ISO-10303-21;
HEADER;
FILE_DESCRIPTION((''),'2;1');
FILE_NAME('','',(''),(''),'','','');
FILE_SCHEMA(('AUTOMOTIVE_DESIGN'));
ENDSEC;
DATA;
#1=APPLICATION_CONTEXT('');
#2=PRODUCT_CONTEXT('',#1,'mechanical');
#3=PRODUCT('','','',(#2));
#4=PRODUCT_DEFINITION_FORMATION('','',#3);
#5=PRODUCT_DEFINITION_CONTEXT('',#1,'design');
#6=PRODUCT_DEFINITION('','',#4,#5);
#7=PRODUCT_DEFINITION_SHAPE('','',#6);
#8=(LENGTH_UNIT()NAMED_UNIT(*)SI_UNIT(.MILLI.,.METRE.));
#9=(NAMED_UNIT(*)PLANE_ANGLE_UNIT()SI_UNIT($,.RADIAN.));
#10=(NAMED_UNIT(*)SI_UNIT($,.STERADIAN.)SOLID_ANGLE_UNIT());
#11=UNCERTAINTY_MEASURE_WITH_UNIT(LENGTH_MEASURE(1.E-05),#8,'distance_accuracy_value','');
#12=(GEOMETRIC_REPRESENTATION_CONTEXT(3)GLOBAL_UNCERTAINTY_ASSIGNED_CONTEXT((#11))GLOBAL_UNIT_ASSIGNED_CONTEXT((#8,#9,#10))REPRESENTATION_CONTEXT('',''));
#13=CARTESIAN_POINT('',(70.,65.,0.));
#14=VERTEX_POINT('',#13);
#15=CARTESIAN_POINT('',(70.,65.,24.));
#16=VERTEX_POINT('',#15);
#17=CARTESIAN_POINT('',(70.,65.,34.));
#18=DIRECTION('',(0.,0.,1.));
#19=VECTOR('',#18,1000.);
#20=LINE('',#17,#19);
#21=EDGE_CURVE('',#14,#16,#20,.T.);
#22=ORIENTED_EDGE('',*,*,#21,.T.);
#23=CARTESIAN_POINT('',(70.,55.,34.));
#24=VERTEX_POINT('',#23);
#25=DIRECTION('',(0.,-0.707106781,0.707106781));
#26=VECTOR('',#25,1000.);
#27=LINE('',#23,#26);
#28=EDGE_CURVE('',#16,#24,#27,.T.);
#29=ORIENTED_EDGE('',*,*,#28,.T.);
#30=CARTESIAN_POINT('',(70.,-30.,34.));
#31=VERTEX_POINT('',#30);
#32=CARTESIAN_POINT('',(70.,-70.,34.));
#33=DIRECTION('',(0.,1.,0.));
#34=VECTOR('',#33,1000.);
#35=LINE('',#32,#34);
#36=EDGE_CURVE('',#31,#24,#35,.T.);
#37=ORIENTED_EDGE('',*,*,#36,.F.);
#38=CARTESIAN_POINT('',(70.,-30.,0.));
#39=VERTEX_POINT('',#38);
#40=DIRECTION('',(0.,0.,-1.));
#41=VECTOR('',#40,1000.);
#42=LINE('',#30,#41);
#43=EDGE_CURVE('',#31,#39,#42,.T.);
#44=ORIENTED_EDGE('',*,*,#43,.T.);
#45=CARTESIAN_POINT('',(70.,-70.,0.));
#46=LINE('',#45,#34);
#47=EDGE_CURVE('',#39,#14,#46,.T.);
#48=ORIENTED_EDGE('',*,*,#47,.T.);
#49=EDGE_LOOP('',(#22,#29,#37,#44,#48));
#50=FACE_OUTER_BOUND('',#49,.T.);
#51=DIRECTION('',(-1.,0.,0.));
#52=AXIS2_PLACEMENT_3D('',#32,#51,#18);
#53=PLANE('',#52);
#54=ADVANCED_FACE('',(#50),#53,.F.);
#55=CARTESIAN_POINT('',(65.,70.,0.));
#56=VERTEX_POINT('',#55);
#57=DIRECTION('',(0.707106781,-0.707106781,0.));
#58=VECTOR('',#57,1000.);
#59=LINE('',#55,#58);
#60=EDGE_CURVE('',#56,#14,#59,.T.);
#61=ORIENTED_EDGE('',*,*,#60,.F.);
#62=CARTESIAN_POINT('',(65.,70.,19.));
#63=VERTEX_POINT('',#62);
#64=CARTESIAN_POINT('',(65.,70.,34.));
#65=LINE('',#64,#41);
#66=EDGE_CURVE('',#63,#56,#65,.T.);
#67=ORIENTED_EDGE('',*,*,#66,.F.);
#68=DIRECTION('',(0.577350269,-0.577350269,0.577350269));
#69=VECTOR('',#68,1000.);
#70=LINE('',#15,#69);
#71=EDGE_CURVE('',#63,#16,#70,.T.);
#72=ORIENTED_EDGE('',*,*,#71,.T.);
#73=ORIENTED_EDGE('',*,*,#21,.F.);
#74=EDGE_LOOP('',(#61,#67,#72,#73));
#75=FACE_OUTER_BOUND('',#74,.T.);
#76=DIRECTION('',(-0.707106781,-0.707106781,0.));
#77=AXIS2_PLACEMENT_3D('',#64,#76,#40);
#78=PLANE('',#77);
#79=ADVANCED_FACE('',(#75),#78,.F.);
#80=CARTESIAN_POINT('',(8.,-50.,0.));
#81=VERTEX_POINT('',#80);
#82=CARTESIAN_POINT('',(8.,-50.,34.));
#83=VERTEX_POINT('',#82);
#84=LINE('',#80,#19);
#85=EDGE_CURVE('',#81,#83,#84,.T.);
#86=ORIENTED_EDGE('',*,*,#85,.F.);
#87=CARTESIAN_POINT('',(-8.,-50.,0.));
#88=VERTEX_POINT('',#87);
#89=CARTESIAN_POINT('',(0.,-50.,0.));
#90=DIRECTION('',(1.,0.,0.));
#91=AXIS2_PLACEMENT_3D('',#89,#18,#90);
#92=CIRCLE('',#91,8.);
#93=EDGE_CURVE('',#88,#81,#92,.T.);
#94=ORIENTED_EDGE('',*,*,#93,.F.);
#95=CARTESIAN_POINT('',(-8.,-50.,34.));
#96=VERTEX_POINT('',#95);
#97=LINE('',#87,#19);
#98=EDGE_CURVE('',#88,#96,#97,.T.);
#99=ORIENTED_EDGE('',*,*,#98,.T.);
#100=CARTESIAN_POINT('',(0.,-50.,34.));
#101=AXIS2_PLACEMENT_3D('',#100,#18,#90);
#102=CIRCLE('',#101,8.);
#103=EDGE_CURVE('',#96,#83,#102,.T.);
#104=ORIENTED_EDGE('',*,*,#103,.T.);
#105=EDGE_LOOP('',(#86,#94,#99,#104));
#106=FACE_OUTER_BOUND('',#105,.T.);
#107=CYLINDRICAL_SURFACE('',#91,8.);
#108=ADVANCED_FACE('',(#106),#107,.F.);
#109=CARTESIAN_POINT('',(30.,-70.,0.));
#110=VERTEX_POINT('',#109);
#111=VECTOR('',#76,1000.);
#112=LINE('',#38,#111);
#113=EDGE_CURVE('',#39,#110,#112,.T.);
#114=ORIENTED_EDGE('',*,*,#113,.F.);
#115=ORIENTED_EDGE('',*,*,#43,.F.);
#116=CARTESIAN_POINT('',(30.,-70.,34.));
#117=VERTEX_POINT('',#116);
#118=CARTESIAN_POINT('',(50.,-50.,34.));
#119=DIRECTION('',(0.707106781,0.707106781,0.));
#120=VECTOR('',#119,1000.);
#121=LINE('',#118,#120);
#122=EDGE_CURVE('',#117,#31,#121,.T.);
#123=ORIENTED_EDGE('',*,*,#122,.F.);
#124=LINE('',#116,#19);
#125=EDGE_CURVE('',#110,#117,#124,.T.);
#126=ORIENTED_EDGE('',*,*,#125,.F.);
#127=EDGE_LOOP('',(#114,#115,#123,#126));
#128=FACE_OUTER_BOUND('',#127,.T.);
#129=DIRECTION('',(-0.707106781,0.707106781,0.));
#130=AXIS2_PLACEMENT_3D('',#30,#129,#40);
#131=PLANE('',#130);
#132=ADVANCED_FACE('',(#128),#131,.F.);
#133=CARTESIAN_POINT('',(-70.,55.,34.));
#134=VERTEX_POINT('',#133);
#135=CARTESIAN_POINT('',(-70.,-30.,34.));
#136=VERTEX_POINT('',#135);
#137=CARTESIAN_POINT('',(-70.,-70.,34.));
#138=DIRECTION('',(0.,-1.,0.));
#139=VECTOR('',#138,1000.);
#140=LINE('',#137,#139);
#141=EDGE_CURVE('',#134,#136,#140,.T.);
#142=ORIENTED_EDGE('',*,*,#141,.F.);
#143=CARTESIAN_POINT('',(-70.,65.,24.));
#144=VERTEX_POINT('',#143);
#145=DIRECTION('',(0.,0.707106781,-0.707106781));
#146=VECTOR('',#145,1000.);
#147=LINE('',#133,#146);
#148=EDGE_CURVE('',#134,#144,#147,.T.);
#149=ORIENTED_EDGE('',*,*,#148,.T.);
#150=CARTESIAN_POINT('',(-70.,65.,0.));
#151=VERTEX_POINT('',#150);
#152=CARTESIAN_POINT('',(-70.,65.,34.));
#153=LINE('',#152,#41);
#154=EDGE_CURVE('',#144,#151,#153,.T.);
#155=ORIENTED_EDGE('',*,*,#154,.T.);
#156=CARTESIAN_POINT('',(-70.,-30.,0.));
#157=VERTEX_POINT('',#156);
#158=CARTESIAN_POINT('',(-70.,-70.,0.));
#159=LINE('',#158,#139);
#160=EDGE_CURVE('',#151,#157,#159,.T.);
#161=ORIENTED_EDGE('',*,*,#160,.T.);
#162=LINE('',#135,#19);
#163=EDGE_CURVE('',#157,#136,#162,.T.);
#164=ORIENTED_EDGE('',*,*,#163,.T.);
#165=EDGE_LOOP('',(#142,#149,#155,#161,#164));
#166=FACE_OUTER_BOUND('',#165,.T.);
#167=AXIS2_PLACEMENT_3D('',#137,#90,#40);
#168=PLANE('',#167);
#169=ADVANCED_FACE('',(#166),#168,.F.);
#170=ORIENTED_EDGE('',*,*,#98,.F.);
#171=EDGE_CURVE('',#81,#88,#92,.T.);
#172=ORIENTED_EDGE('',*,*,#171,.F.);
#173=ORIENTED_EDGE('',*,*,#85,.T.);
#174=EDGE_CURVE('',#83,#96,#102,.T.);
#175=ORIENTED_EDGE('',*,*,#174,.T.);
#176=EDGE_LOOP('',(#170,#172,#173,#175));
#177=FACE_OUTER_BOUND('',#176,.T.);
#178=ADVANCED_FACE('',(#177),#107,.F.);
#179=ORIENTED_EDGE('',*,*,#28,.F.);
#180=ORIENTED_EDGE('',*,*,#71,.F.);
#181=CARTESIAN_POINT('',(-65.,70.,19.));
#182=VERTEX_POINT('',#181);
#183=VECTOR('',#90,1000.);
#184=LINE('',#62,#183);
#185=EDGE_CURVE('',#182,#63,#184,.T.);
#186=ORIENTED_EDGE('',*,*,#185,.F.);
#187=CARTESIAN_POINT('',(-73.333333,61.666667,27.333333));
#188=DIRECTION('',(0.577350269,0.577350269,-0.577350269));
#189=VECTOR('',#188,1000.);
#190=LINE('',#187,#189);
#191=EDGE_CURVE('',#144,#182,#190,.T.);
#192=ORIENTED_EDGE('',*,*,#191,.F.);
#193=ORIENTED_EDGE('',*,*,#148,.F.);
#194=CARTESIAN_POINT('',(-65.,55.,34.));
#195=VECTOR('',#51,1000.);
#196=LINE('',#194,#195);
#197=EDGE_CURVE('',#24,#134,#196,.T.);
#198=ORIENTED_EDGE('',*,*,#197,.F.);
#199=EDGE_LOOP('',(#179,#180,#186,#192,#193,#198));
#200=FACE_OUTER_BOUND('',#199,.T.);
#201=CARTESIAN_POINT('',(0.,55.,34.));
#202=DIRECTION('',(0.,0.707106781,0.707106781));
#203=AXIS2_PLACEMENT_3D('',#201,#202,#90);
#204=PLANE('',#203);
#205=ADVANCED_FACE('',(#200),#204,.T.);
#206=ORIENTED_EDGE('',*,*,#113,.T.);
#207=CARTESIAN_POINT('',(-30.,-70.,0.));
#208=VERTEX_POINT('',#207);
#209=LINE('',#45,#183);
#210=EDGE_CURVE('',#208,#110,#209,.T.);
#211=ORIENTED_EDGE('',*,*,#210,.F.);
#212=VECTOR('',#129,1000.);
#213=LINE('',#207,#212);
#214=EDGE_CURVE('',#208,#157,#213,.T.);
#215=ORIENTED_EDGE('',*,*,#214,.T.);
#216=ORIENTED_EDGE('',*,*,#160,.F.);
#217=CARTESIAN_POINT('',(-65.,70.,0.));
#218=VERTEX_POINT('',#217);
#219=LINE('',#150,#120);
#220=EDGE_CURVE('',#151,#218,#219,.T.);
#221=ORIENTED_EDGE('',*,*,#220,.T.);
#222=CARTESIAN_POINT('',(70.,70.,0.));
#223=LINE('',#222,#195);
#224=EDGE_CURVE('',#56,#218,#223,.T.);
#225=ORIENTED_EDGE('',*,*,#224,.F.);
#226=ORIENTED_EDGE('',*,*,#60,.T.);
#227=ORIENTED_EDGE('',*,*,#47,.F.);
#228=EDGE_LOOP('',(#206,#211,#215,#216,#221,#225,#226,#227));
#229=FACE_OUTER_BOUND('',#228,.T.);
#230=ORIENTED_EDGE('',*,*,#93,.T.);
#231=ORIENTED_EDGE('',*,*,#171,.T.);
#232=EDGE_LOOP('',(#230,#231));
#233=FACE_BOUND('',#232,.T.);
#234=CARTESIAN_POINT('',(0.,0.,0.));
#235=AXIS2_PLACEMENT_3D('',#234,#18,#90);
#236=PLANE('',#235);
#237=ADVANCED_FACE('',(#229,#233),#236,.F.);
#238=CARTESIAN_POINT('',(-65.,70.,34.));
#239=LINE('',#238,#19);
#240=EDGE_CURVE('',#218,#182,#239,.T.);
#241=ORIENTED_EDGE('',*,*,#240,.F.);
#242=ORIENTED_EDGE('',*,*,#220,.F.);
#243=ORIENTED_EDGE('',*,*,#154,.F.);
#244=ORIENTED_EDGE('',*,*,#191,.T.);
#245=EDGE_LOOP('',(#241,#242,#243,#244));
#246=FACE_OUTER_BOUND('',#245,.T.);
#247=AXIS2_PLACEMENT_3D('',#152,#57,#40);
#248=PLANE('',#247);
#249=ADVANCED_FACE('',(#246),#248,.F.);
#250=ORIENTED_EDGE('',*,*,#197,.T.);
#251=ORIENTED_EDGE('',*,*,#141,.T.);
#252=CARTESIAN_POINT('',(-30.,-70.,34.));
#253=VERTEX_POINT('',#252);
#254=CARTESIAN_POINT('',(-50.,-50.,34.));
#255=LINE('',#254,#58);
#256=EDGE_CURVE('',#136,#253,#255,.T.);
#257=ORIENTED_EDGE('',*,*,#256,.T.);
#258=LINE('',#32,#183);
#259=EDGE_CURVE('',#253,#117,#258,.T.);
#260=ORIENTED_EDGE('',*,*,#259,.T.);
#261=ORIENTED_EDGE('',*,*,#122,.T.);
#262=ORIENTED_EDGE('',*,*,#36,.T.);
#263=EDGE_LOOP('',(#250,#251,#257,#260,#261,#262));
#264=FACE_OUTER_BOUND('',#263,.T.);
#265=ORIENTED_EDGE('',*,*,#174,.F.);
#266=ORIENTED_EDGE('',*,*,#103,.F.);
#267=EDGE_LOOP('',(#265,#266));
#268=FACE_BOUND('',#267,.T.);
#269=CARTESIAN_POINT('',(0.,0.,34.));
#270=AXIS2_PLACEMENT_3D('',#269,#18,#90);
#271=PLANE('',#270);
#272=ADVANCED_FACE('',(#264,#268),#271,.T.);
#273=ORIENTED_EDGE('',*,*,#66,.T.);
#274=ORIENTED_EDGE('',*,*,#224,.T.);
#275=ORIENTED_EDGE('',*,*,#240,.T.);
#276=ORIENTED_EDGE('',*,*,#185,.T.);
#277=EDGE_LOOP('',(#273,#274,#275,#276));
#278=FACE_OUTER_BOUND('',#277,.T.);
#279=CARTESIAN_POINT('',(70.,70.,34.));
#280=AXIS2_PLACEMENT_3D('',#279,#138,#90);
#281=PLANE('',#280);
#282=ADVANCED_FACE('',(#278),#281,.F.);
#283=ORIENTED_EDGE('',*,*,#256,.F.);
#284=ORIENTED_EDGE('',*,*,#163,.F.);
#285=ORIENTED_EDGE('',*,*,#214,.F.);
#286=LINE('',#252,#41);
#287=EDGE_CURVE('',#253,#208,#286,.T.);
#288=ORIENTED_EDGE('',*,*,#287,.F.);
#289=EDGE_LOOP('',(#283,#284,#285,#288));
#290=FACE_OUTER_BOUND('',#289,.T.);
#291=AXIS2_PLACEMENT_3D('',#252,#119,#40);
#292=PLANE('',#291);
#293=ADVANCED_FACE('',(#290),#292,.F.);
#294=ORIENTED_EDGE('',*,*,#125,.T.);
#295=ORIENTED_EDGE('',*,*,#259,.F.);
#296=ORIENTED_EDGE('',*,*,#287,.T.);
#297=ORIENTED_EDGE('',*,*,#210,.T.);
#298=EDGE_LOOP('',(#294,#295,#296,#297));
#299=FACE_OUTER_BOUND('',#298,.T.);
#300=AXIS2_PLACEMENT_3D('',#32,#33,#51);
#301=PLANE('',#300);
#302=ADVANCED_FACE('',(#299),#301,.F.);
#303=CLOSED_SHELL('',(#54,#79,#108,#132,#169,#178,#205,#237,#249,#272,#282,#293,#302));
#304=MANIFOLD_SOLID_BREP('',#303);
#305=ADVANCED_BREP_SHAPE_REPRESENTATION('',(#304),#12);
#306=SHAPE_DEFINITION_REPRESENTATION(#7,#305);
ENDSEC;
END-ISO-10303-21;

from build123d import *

# Parameters (mm, degrees)
SKETCH1_W           = 140
SKETCH1_H           = 140
BOSS_EXTRUDE1_DEPTH = 34
SKETCH3_R           = 8
CUT_EXTRUDE3_DEPTH  = 105.670912865
CHAMFER1_SIZE       = 5
CHAMFER2_SIZE       = 15
CHAMFER3_SIZE       = 40


with BuildPart() as part:
    # Sketch1 → Boss-Extrude1 (new body)
    with BuildSketch(Plane.XY):
        Rectangle(SKETCH1_W, SKETCH1_H)
    extrude(amount=BOSS_EXTRUDE1_DEPTH)

    # Sketch3 → Cut-Extrude3 (cut, through all)
    with BuildSketch(Plane.XY.offset(34)):
        with Locations((0, -50)):
            Circle(SKETCH3_R)
    extrude(amount=-CUT_EXTRUDE3_DEPTH, mode=Mode.SUBTRACT)

    # Chamfer1
    chamfer1_edges = [part.edges().sort_by_distance(p)[0] for p in [
        (-70, 70, 17),
        (70, 70, 17),
    ]]
    chamfer(chamfer1_edges, length=CHAMFER1_SIZE)

    # Chamfer2
    chamfer2_edges = [part.edges().sort_by_distance(p)[0] for p in [
        (0, 70, 34),
    ]]
    chamfer(chamfer2_edges, length=CHAMFER2_SIZE)

    # Chamfer3
    chamfer3_edges = [part.edges().sort_by_distance(p)[0] for p in [
        (70, -70, 17),
        (-70, -70, 17),
    ]]
    chamfer(chamfer3_edges, length=CHAMFER3_SIZE)


solid = part.part
